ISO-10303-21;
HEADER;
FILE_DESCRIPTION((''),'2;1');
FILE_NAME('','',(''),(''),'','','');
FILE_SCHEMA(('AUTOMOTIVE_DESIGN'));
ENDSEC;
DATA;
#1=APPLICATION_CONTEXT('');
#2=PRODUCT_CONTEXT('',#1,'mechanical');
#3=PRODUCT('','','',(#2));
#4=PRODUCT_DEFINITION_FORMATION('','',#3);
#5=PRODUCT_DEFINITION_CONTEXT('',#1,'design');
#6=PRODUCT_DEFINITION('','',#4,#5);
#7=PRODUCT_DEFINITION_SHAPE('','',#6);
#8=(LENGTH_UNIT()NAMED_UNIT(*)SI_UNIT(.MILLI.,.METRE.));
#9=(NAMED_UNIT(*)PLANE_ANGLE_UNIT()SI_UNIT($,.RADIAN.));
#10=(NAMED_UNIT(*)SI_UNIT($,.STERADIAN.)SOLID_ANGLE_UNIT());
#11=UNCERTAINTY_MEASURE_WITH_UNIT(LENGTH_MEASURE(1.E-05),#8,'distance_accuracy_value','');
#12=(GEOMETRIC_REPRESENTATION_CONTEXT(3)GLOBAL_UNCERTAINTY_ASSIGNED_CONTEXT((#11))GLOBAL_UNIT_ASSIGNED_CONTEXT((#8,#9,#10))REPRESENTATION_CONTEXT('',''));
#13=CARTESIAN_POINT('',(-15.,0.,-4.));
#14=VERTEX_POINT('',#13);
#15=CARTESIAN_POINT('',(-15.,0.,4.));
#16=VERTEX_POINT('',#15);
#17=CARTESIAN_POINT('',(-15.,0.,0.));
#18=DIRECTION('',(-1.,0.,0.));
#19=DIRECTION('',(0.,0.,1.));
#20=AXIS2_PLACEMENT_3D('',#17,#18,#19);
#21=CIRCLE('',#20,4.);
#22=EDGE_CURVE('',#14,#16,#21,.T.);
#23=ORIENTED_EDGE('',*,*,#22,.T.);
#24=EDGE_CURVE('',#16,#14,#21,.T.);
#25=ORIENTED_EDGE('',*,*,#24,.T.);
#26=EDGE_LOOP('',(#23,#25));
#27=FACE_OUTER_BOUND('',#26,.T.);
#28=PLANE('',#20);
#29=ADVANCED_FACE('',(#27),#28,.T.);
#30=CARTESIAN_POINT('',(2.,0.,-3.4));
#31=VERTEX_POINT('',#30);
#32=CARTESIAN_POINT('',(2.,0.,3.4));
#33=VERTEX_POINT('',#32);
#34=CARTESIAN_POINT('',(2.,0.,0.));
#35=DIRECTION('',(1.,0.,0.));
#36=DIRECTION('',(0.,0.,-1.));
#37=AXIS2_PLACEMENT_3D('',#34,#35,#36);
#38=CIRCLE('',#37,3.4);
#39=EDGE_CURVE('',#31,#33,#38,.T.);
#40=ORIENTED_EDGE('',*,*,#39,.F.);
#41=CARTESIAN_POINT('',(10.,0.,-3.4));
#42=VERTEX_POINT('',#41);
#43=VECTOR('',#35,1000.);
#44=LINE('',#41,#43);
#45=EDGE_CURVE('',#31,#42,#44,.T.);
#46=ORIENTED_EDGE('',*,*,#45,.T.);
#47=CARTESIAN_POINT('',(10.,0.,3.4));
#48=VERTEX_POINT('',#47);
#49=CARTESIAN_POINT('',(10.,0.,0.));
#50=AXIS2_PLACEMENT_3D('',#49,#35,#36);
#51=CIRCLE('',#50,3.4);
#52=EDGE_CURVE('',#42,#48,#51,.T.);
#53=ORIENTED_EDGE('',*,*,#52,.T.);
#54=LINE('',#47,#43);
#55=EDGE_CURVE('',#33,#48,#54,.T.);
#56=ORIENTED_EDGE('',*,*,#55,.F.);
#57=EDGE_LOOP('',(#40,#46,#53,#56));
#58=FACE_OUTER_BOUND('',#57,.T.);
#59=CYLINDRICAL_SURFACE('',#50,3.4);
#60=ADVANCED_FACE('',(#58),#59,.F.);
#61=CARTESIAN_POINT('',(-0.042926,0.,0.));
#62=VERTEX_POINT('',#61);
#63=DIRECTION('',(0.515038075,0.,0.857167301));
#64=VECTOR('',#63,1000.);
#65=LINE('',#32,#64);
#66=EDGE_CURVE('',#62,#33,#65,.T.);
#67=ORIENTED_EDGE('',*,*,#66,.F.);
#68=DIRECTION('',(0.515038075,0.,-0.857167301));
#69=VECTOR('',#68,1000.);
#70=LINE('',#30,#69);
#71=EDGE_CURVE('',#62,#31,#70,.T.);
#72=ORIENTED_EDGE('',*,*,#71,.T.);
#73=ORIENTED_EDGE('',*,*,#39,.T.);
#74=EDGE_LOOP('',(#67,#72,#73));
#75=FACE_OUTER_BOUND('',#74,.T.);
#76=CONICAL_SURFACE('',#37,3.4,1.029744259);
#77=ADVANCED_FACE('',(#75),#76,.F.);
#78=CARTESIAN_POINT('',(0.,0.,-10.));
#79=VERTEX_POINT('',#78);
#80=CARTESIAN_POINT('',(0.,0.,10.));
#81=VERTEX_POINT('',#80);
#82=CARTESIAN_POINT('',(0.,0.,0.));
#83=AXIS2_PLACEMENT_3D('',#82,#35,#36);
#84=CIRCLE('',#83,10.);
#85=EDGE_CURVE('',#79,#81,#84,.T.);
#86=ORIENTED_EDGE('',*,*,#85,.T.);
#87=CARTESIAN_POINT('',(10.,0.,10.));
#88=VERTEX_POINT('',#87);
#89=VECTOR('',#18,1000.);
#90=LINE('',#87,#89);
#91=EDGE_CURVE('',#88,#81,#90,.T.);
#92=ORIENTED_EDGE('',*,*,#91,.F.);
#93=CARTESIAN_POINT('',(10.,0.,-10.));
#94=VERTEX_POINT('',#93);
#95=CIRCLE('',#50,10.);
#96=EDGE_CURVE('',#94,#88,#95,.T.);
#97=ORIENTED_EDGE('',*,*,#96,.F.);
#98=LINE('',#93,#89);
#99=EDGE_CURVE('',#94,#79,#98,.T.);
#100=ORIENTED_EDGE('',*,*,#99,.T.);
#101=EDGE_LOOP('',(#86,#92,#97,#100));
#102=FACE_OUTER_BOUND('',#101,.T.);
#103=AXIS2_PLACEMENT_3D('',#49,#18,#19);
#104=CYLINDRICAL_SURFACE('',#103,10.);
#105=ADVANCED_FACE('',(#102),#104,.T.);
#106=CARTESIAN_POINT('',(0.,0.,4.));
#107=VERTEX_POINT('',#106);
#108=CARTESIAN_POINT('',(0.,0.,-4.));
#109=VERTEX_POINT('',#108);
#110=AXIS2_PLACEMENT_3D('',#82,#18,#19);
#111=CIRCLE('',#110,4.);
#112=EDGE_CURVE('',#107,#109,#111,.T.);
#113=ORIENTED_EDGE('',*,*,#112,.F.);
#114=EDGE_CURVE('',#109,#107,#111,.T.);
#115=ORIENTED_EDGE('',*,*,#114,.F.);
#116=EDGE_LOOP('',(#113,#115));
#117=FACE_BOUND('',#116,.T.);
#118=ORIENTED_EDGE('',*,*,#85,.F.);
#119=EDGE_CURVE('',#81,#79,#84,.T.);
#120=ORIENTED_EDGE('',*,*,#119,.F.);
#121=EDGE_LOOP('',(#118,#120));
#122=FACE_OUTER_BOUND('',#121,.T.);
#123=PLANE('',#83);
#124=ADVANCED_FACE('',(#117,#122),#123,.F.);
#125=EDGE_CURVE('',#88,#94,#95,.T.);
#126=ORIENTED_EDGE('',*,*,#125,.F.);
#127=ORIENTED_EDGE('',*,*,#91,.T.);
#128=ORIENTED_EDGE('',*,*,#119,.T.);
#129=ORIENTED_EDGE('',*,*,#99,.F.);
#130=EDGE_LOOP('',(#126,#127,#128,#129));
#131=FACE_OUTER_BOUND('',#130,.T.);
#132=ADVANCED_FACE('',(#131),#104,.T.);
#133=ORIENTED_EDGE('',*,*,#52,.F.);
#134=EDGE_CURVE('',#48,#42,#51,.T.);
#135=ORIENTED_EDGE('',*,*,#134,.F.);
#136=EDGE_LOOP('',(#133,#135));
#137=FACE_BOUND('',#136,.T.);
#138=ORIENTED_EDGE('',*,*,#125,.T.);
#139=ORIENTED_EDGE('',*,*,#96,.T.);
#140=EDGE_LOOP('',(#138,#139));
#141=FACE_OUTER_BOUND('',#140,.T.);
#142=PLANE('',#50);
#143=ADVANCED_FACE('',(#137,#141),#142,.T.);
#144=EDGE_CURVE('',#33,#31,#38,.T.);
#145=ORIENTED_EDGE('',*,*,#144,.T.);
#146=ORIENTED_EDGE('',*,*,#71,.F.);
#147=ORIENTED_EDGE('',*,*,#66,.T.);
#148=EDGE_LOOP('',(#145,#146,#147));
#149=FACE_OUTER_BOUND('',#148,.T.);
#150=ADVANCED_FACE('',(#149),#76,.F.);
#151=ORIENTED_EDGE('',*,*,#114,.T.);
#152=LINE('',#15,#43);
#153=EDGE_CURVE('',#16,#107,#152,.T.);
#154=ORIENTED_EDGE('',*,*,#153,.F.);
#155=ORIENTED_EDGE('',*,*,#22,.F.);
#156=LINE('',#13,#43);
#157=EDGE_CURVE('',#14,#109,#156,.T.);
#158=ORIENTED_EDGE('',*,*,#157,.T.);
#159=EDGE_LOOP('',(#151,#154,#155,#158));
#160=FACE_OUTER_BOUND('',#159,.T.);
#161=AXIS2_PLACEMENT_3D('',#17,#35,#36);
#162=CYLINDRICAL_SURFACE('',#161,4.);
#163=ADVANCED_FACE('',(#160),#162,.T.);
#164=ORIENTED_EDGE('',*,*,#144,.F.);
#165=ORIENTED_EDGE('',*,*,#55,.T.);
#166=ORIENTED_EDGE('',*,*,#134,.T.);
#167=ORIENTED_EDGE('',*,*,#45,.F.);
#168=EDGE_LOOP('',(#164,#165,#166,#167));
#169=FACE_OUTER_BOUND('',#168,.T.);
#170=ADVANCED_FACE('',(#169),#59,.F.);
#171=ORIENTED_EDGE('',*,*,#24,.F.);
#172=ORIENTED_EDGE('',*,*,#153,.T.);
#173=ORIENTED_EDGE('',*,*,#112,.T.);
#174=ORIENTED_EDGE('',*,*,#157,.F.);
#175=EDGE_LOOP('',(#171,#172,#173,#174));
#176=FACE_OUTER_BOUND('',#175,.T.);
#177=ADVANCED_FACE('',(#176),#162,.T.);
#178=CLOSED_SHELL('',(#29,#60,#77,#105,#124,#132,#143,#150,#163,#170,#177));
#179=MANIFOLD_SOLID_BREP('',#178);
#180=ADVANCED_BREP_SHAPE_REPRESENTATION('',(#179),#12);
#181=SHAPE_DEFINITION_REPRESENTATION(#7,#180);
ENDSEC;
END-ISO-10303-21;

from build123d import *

# Parameters (mm, degrees)
SKETCH_1_R             = 10
EXTRUDE_1_DEPTH        = 10
SKETCH_2_R             = 4
EXTRUDE_2_DEPTH        = 15
HOLE_WIZARD_M8_1_D     = 6.8
HOLE_WIZARD_M8_1_DEPTH = 8
HOLE_WIZARD_M8_1_TIP   = 2.042926105


with BuildPart() as part:
    # 草图1 → 凸台-拉伸1 (new body)
    with BuildSketch(Plane(origin=(0, 0, 0), x_dir=(0, 0, -1), z_dir=(1, 0, 0))):
        Circle(SKETCH_1_R)
    extrude(amount=EXTRUDE_1_DEPTH)

    # 草图2 → 凸台-拉伸2 (add)
    with BuildSketch(Plane.ZY):
        Circle(SKETCH_2_R)
    extrude(amount=EXTRUDE_2_DEPTH)

    # M8 螺纹孔1
    with Locations(Plane(origin=(10, 0, 0), x_dir=(0, 0, -1), z_dir=(1, 0, 0))):
        with Locations((0, 0)):
            Hole(HOLE_WIZARD_M8_1_D / 2, depth=HOLE_WIZARD_M8_1_DEPTH)
            with Locations((0, 0, -(HOLE_WIZARD_M8_1_DEPTH + HOLE_WIZARD_M8_1_TIP / 2))):  # 118° drill point
                Cone(0, HOLE_WIZARD_M8_1_D / 2, HOLE_WIZARD_M8_1_TIP, mode=Mode.SUBTRACT)


solid = part.part
